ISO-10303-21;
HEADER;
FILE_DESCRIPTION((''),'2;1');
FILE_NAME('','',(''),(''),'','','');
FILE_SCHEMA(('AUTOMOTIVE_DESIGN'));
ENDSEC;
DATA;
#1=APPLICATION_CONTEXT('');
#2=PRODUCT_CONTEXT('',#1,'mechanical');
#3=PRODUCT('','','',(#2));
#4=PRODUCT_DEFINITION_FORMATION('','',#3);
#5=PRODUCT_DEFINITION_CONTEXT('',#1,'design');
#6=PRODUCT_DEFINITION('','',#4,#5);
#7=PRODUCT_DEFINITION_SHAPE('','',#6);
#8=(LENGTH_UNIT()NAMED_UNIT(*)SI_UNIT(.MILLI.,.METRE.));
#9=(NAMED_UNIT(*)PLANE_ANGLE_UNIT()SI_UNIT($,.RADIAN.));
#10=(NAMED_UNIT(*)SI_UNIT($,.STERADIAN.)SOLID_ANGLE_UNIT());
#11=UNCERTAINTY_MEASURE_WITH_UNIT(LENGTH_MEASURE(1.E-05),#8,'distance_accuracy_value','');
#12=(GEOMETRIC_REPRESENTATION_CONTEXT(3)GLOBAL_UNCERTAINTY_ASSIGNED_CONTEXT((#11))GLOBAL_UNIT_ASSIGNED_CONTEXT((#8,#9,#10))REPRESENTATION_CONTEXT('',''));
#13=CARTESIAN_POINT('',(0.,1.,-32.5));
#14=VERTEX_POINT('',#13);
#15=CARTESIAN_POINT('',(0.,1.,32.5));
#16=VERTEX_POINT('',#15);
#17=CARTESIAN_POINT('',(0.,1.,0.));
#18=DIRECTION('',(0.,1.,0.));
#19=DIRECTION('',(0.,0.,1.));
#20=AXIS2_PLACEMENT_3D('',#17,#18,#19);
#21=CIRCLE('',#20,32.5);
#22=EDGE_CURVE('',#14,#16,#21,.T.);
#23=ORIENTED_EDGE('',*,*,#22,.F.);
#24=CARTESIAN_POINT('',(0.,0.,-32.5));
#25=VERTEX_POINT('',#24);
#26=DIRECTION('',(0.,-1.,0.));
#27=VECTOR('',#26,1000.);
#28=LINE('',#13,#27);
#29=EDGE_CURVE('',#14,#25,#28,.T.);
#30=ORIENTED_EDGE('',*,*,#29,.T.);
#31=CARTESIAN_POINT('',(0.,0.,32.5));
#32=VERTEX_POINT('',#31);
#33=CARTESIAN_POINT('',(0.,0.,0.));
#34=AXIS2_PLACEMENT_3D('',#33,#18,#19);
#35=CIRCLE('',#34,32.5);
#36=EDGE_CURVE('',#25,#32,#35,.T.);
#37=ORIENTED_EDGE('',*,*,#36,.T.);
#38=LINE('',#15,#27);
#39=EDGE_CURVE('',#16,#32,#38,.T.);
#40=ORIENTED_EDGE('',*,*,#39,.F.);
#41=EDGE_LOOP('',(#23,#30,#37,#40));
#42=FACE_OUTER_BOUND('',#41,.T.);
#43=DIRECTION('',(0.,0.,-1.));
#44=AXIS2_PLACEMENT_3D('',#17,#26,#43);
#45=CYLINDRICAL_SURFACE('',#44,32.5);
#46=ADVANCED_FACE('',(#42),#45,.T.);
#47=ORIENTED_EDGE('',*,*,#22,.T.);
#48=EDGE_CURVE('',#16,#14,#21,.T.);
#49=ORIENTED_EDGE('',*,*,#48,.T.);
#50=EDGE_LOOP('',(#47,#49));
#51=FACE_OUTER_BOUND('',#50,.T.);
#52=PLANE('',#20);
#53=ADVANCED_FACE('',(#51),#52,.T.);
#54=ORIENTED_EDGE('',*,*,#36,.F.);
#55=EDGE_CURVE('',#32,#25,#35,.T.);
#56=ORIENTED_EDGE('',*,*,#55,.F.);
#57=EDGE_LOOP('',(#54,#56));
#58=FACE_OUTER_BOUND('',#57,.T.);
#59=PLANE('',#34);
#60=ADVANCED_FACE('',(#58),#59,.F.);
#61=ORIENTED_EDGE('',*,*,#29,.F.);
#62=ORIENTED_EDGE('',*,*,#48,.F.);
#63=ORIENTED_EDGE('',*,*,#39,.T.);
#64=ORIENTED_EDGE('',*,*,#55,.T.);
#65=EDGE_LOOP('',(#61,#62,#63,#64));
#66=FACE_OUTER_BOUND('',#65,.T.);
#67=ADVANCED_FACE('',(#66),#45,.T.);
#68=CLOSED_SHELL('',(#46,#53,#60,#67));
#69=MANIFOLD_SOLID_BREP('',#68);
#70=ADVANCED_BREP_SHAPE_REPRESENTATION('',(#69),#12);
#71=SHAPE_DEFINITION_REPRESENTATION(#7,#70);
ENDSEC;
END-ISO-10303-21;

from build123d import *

# Parameters (mm, degrees)
SKETCH1_R           = 32.5
BOSS_EXTRUDE1_DEPTH = 1


with BuildPart() as part:
    # Sketch1 → Boss-Extrude1 (new body)
    with BuildSketch(Plane(origin=(0, 0, 0), x_dir=(1, 0, 0), z_dir=(0, 1, 0))):
        with Locations(Location((0, 0, 0), (0, 0, 270))):
            Circle(SKETCH1_R)
    extrude(amount=BOSS_EXTRUDE1_DEPTH)


solid = part.part
